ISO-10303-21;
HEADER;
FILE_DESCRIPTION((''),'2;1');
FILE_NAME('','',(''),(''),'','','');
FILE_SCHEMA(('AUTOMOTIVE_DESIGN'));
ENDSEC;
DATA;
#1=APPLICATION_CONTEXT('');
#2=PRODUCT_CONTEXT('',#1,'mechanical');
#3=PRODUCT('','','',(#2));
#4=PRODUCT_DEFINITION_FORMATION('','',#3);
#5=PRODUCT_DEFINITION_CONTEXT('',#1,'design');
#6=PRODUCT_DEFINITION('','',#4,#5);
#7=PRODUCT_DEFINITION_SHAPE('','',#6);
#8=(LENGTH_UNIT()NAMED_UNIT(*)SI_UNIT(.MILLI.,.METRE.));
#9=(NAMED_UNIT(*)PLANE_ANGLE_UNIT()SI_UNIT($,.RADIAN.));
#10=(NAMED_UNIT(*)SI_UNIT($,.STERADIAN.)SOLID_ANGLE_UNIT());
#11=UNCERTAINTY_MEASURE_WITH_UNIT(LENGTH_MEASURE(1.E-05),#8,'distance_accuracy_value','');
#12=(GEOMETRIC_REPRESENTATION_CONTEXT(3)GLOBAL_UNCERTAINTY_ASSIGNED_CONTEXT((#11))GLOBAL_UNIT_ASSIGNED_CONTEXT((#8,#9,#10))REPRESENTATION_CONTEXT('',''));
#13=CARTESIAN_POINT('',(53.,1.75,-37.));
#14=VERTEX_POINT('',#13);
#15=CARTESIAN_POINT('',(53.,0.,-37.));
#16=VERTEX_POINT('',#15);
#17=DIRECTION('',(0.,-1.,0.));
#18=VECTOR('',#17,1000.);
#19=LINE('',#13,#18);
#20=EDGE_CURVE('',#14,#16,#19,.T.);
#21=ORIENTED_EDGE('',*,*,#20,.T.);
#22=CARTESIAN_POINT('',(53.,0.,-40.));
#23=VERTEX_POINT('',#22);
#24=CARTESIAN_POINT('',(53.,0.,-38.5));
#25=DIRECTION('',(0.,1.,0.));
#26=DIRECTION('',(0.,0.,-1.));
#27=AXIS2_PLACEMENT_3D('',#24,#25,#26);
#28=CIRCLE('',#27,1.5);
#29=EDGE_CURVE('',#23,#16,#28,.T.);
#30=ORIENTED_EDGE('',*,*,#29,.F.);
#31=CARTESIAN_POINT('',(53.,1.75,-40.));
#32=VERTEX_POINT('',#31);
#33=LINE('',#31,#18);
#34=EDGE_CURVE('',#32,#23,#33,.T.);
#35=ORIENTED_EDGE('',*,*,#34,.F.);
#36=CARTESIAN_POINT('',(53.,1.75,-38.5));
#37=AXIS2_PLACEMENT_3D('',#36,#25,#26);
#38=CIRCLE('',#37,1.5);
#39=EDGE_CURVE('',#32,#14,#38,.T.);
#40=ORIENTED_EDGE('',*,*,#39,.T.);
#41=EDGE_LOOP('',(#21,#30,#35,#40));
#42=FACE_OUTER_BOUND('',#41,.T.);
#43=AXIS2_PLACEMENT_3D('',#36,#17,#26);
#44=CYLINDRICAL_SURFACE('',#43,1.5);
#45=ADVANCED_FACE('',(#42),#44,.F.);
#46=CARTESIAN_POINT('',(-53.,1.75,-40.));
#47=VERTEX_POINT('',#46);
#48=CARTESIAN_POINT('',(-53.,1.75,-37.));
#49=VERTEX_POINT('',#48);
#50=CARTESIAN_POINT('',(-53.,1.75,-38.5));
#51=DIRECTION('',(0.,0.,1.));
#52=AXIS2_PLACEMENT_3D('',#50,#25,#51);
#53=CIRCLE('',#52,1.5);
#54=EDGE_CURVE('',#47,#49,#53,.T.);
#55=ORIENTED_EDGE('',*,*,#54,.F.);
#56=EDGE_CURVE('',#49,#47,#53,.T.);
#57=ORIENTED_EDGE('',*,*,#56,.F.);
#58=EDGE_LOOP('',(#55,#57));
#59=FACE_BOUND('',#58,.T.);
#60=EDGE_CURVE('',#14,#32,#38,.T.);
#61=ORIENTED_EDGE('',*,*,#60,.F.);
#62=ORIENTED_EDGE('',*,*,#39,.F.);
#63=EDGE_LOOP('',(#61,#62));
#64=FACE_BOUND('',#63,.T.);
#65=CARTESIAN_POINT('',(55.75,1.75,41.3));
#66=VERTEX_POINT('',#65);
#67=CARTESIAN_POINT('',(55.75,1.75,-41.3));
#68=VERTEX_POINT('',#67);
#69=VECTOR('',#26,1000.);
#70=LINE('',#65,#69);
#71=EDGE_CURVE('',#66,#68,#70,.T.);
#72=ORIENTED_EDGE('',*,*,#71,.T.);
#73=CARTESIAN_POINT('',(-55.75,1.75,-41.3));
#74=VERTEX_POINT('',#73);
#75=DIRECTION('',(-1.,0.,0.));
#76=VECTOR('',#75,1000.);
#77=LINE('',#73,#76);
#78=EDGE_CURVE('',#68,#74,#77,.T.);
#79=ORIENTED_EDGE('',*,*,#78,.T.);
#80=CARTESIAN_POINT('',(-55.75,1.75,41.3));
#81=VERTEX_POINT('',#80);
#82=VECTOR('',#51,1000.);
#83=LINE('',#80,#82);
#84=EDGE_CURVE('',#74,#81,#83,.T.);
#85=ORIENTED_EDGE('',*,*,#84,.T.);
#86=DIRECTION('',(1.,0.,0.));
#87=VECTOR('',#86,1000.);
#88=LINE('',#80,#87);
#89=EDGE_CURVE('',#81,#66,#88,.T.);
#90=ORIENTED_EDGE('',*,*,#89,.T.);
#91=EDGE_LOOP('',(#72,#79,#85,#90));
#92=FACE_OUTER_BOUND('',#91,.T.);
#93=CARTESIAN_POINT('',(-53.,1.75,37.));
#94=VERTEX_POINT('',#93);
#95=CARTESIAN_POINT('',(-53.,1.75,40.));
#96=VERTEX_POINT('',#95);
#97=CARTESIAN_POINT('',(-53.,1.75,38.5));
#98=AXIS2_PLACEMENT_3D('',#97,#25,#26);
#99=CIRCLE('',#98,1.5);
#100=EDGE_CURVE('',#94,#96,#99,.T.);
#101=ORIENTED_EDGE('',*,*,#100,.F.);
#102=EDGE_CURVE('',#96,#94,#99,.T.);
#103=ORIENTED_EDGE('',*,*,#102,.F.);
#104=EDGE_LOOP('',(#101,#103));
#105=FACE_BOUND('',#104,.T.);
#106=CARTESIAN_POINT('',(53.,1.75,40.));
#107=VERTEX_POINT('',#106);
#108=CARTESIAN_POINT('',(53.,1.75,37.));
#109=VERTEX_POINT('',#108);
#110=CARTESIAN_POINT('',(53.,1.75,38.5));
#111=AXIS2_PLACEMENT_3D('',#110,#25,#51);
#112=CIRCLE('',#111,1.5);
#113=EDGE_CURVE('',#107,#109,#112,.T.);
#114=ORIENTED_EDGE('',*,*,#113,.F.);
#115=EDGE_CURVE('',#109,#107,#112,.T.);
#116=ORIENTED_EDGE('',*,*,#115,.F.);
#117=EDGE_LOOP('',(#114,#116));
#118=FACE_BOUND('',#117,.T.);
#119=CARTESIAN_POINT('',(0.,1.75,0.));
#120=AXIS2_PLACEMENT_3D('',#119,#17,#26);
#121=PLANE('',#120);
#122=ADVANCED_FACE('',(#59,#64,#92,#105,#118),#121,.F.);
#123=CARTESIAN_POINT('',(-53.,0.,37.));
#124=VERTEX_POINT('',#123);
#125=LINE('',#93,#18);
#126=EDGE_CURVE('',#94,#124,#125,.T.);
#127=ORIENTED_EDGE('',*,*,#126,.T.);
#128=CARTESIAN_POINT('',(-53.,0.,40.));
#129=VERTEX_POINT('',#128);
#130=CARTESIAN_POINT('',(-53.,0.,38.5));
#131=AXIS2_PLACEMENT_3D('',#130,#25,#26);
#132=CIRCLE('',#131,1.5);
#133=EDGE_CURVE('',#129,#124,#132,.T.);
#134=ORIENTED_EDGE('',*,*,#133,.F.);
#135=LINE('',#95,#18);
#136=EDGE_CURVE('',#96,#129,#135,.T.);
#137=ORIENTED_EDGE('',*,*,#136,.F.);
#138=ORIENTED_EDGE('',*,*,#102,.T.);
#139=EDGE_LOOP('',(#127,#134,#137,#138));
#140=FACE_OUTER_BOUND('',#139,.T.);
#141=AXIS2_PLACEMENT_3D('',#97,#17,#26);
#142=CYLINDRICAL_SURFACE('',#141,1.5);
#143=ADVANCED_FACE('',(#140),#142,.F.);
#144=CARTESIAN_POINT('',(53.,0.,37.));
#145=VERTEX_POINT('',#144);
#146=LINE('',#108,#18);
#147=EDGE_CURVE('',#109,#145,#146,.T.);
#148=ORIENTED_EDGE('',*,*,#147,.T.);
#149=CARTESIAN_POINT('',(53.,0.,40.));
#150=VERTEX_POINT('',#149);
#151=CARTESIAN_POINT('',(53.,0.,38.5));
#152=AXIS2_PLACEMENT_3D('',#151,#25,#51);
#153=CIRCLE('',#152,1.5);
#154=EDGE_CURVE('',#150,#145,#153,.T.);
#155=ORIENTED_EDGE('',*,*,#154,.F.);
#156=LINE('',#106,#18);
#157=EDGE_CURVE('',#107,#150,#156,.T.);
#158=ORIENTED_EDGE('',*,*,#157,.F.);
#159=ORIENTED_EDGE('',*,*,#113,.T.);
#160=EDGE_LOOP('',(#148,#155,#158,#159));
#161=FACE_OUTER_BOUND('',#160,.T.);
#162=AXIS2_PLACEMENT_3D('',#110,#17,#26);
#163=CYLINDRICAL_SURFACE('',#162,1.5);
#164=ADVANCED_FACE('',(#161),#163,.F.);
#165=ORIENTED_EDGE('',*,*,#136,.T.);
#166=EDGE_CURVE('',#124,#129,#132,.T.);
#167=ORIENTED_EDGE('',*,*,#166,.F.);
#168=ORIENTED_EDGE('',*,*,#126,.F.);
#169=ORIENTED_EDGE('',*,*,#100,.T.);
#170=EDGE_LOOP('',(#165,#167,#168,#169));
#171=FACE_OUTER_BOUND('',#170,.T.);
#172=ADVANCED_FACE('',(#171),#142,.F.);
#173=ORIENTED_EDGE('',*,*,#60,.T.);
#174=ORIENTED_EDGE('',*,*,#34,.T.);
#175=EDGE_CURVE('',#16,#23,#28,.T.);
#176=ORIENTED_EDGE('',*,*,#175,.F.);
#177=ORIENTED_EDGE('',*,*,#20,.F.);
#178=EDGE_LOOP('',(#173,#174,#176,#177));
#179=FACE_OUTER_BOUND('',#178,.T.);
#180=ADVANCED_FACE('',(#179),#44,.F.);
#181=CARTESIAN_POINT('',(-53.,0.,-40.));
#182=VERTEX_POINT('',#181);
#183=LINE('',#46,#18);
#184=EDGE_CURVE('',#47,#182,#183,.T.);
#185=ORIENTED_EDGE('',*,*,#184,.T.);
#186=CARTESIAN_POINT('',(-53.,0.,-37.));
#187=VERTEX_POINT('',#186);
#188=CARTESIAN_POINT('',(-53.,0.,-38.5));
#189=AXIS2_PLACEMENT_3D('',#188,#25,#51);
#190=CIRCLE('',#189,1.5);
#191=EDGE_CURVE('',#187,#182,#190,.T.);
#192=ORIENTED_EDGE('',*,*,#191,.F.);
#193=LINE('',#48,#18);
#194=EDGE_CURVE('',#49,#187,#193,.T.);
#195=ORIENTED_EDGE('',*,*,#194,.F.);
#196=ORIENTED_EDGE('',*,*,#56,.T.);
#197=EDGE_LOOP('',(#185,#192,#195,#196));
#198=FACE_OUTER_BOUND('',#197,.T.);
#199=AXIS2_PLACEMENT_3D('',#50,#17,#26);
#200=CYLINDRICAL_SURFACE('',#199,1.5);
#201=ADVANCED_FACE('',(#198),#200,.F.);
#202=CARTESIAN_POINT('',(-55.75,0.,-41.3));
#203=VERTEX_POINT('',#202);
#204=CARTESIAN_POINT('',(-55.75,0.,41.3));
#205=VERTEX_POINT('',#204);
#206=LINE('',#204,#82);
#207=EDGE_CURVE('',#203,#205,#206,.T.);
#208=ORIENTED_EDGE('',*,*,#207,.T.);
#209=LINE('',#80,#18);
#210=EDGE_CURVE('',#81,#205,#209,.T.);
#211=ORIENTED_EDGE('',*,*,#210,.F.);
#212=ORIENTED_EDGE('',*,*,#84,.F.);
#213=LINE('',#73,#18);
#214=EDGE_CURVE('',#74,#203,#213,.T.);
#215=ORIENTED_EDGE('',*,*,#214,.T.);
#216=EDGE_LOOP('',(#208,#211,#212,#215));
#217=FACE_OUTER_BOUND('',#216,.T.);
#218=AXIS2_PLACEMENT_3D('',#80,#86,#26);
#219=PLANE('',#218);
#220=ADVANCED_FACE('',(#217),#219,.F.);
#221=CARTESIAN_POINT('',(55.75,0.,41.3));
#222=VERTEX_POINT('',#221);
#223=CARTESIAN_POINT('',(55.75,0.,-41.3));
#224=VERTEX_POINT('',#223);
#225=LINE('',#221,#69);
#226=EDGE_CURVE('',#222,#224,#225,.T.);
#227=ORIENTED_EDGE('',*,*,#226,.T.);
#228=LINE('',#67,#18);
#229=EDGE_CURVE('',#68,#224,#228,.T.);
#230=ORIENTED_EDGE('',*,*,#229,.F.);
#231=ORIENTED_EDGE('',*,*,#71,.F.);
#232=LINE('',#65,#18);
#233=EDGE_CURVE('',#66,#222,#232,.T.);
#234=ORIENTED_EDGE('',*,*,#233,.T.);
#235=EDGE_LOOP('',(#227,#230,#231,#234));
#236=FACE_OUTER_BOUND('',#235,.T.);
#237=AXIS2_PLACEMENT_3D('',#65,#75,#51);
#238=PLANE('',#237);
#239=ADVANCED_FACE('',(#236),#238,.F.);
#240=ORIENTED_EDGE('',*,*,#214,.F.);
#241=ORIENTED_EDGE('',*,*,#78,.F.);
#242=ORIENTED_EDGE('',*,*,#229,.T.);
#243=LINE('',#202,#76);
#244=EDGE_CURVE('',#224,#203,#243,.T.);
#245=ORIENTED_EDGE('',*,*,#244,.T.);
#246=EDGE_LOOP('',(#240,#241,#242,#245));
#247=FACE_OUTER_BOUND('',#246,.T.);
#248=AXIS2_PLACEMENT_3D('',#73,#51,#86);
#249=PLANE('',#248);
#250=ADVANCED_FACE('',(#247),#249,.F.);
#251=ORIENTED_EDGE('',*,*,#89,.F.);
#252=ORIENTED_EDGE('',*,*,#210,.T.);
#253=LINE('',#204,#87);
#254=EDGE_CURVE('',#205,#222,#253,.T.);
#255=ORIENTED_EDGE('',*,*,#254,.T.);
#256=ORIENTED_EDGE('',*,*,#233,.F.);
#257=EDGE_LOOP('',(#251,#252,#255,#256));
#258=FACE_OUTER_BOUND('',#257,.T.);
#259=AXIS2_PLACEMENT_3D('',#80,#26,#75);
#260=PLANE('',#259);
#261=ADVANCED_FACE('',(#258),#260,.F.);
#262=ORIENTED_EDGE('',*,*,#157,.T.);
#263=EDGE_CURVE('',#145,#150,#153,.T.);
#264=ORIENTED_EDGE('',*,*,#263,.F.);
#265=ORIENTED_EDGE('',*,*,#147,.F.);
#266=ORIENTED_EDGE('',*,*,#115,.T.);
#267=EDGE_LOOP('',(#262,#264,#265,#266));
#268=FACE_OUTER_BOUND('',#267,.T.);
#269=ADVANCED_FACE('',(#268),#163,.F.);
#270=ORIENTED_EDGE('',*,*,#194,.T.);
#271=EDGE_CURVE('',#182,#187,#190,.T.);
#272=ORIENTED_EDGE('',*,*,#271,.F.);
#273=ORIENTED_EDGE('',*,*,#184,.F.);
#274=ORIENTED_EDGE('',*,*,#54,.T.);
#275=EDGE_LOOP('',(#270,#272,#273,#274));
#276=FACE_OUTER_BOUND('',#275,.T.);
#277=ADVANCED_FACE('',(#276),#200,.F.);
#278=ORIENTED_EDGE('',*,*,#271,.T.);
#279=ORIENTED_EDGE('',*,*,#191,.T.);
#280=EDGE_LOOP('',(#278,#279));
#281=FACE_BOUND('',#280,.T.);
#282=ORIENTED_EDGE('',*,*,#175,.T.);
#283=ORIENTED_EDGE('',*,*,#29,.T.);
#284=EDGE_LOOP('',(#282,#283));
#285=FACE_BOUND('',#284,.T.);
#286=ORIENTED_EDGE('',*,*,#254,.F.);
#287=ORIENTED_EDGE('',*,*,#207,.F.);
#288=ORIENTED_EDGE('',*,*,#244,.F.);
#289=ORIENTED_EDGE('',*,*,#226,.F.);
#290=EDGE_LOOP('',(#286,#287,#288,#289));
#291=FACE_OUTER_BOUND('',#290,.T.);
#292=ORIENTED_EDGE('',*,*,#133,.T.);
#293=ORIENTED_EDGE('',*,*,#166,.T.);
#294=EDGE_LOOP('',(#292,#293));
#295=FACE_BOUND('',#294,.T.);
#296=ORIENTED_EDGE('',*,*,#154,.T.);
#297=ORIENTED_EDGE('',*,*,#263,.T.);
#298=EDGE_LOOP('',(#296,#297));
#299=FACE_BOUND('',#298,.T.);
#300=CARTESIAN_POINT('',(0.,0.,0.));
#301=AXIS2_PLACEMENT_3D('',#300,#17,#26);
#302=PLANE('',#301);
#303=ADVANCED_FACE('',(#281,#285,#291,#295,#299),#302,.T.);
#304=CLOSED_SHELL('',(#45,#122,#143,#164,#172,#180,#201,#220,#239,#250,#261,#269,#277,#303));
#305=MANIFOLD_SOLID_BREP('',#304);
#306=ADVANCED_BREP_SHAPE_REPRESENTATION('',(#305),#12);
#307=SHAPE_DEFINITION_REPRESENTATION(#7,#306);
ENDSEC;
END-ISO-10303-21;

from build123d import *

# Parameters (mm, degrees)
SKETCH_1_W      = 111.5
SKETCH_1_H      = 82.6
SKETCH_1_R      = 1.5
EXTRUDE_1_DEPTH = 1.75


with BuildPart() as part:
    # 草图1 → 凸台-拉伸1 (new body)
    with BuildSketch(Plane(origin=(0, 0, 0), x_dir=(1, 0, 0), z_dir=(0, 1, 0))):
        Rectangle(SKETCH_1_W, SKETCH_1_H)
        with Locations(Location((-53, 38.5, 0), (0, 0, 270))):
            Circle(SKETCH_1_R, mode=Mode.SUBTRACT)
        with Locations(Location((53, 38.5, 0), (0, 0, 90))):
            Circle(SKETCH_1_R, mode=Mode.SUBTRACT)
        with Locations(Location((53, -38.5, 0), (0, 0, 270))):
            Circle(SKETCH_1_R, mode=Mode.SUBTRACT)
        with Locations(Location((-53, -38.5, 0), (0, 0, 90))):
            Circle(SKETCH_1_R, mode=Mode.SUBTRACT)
    extrude(amount=EXTRUDE_1_DEPTH)


solid = part.part
